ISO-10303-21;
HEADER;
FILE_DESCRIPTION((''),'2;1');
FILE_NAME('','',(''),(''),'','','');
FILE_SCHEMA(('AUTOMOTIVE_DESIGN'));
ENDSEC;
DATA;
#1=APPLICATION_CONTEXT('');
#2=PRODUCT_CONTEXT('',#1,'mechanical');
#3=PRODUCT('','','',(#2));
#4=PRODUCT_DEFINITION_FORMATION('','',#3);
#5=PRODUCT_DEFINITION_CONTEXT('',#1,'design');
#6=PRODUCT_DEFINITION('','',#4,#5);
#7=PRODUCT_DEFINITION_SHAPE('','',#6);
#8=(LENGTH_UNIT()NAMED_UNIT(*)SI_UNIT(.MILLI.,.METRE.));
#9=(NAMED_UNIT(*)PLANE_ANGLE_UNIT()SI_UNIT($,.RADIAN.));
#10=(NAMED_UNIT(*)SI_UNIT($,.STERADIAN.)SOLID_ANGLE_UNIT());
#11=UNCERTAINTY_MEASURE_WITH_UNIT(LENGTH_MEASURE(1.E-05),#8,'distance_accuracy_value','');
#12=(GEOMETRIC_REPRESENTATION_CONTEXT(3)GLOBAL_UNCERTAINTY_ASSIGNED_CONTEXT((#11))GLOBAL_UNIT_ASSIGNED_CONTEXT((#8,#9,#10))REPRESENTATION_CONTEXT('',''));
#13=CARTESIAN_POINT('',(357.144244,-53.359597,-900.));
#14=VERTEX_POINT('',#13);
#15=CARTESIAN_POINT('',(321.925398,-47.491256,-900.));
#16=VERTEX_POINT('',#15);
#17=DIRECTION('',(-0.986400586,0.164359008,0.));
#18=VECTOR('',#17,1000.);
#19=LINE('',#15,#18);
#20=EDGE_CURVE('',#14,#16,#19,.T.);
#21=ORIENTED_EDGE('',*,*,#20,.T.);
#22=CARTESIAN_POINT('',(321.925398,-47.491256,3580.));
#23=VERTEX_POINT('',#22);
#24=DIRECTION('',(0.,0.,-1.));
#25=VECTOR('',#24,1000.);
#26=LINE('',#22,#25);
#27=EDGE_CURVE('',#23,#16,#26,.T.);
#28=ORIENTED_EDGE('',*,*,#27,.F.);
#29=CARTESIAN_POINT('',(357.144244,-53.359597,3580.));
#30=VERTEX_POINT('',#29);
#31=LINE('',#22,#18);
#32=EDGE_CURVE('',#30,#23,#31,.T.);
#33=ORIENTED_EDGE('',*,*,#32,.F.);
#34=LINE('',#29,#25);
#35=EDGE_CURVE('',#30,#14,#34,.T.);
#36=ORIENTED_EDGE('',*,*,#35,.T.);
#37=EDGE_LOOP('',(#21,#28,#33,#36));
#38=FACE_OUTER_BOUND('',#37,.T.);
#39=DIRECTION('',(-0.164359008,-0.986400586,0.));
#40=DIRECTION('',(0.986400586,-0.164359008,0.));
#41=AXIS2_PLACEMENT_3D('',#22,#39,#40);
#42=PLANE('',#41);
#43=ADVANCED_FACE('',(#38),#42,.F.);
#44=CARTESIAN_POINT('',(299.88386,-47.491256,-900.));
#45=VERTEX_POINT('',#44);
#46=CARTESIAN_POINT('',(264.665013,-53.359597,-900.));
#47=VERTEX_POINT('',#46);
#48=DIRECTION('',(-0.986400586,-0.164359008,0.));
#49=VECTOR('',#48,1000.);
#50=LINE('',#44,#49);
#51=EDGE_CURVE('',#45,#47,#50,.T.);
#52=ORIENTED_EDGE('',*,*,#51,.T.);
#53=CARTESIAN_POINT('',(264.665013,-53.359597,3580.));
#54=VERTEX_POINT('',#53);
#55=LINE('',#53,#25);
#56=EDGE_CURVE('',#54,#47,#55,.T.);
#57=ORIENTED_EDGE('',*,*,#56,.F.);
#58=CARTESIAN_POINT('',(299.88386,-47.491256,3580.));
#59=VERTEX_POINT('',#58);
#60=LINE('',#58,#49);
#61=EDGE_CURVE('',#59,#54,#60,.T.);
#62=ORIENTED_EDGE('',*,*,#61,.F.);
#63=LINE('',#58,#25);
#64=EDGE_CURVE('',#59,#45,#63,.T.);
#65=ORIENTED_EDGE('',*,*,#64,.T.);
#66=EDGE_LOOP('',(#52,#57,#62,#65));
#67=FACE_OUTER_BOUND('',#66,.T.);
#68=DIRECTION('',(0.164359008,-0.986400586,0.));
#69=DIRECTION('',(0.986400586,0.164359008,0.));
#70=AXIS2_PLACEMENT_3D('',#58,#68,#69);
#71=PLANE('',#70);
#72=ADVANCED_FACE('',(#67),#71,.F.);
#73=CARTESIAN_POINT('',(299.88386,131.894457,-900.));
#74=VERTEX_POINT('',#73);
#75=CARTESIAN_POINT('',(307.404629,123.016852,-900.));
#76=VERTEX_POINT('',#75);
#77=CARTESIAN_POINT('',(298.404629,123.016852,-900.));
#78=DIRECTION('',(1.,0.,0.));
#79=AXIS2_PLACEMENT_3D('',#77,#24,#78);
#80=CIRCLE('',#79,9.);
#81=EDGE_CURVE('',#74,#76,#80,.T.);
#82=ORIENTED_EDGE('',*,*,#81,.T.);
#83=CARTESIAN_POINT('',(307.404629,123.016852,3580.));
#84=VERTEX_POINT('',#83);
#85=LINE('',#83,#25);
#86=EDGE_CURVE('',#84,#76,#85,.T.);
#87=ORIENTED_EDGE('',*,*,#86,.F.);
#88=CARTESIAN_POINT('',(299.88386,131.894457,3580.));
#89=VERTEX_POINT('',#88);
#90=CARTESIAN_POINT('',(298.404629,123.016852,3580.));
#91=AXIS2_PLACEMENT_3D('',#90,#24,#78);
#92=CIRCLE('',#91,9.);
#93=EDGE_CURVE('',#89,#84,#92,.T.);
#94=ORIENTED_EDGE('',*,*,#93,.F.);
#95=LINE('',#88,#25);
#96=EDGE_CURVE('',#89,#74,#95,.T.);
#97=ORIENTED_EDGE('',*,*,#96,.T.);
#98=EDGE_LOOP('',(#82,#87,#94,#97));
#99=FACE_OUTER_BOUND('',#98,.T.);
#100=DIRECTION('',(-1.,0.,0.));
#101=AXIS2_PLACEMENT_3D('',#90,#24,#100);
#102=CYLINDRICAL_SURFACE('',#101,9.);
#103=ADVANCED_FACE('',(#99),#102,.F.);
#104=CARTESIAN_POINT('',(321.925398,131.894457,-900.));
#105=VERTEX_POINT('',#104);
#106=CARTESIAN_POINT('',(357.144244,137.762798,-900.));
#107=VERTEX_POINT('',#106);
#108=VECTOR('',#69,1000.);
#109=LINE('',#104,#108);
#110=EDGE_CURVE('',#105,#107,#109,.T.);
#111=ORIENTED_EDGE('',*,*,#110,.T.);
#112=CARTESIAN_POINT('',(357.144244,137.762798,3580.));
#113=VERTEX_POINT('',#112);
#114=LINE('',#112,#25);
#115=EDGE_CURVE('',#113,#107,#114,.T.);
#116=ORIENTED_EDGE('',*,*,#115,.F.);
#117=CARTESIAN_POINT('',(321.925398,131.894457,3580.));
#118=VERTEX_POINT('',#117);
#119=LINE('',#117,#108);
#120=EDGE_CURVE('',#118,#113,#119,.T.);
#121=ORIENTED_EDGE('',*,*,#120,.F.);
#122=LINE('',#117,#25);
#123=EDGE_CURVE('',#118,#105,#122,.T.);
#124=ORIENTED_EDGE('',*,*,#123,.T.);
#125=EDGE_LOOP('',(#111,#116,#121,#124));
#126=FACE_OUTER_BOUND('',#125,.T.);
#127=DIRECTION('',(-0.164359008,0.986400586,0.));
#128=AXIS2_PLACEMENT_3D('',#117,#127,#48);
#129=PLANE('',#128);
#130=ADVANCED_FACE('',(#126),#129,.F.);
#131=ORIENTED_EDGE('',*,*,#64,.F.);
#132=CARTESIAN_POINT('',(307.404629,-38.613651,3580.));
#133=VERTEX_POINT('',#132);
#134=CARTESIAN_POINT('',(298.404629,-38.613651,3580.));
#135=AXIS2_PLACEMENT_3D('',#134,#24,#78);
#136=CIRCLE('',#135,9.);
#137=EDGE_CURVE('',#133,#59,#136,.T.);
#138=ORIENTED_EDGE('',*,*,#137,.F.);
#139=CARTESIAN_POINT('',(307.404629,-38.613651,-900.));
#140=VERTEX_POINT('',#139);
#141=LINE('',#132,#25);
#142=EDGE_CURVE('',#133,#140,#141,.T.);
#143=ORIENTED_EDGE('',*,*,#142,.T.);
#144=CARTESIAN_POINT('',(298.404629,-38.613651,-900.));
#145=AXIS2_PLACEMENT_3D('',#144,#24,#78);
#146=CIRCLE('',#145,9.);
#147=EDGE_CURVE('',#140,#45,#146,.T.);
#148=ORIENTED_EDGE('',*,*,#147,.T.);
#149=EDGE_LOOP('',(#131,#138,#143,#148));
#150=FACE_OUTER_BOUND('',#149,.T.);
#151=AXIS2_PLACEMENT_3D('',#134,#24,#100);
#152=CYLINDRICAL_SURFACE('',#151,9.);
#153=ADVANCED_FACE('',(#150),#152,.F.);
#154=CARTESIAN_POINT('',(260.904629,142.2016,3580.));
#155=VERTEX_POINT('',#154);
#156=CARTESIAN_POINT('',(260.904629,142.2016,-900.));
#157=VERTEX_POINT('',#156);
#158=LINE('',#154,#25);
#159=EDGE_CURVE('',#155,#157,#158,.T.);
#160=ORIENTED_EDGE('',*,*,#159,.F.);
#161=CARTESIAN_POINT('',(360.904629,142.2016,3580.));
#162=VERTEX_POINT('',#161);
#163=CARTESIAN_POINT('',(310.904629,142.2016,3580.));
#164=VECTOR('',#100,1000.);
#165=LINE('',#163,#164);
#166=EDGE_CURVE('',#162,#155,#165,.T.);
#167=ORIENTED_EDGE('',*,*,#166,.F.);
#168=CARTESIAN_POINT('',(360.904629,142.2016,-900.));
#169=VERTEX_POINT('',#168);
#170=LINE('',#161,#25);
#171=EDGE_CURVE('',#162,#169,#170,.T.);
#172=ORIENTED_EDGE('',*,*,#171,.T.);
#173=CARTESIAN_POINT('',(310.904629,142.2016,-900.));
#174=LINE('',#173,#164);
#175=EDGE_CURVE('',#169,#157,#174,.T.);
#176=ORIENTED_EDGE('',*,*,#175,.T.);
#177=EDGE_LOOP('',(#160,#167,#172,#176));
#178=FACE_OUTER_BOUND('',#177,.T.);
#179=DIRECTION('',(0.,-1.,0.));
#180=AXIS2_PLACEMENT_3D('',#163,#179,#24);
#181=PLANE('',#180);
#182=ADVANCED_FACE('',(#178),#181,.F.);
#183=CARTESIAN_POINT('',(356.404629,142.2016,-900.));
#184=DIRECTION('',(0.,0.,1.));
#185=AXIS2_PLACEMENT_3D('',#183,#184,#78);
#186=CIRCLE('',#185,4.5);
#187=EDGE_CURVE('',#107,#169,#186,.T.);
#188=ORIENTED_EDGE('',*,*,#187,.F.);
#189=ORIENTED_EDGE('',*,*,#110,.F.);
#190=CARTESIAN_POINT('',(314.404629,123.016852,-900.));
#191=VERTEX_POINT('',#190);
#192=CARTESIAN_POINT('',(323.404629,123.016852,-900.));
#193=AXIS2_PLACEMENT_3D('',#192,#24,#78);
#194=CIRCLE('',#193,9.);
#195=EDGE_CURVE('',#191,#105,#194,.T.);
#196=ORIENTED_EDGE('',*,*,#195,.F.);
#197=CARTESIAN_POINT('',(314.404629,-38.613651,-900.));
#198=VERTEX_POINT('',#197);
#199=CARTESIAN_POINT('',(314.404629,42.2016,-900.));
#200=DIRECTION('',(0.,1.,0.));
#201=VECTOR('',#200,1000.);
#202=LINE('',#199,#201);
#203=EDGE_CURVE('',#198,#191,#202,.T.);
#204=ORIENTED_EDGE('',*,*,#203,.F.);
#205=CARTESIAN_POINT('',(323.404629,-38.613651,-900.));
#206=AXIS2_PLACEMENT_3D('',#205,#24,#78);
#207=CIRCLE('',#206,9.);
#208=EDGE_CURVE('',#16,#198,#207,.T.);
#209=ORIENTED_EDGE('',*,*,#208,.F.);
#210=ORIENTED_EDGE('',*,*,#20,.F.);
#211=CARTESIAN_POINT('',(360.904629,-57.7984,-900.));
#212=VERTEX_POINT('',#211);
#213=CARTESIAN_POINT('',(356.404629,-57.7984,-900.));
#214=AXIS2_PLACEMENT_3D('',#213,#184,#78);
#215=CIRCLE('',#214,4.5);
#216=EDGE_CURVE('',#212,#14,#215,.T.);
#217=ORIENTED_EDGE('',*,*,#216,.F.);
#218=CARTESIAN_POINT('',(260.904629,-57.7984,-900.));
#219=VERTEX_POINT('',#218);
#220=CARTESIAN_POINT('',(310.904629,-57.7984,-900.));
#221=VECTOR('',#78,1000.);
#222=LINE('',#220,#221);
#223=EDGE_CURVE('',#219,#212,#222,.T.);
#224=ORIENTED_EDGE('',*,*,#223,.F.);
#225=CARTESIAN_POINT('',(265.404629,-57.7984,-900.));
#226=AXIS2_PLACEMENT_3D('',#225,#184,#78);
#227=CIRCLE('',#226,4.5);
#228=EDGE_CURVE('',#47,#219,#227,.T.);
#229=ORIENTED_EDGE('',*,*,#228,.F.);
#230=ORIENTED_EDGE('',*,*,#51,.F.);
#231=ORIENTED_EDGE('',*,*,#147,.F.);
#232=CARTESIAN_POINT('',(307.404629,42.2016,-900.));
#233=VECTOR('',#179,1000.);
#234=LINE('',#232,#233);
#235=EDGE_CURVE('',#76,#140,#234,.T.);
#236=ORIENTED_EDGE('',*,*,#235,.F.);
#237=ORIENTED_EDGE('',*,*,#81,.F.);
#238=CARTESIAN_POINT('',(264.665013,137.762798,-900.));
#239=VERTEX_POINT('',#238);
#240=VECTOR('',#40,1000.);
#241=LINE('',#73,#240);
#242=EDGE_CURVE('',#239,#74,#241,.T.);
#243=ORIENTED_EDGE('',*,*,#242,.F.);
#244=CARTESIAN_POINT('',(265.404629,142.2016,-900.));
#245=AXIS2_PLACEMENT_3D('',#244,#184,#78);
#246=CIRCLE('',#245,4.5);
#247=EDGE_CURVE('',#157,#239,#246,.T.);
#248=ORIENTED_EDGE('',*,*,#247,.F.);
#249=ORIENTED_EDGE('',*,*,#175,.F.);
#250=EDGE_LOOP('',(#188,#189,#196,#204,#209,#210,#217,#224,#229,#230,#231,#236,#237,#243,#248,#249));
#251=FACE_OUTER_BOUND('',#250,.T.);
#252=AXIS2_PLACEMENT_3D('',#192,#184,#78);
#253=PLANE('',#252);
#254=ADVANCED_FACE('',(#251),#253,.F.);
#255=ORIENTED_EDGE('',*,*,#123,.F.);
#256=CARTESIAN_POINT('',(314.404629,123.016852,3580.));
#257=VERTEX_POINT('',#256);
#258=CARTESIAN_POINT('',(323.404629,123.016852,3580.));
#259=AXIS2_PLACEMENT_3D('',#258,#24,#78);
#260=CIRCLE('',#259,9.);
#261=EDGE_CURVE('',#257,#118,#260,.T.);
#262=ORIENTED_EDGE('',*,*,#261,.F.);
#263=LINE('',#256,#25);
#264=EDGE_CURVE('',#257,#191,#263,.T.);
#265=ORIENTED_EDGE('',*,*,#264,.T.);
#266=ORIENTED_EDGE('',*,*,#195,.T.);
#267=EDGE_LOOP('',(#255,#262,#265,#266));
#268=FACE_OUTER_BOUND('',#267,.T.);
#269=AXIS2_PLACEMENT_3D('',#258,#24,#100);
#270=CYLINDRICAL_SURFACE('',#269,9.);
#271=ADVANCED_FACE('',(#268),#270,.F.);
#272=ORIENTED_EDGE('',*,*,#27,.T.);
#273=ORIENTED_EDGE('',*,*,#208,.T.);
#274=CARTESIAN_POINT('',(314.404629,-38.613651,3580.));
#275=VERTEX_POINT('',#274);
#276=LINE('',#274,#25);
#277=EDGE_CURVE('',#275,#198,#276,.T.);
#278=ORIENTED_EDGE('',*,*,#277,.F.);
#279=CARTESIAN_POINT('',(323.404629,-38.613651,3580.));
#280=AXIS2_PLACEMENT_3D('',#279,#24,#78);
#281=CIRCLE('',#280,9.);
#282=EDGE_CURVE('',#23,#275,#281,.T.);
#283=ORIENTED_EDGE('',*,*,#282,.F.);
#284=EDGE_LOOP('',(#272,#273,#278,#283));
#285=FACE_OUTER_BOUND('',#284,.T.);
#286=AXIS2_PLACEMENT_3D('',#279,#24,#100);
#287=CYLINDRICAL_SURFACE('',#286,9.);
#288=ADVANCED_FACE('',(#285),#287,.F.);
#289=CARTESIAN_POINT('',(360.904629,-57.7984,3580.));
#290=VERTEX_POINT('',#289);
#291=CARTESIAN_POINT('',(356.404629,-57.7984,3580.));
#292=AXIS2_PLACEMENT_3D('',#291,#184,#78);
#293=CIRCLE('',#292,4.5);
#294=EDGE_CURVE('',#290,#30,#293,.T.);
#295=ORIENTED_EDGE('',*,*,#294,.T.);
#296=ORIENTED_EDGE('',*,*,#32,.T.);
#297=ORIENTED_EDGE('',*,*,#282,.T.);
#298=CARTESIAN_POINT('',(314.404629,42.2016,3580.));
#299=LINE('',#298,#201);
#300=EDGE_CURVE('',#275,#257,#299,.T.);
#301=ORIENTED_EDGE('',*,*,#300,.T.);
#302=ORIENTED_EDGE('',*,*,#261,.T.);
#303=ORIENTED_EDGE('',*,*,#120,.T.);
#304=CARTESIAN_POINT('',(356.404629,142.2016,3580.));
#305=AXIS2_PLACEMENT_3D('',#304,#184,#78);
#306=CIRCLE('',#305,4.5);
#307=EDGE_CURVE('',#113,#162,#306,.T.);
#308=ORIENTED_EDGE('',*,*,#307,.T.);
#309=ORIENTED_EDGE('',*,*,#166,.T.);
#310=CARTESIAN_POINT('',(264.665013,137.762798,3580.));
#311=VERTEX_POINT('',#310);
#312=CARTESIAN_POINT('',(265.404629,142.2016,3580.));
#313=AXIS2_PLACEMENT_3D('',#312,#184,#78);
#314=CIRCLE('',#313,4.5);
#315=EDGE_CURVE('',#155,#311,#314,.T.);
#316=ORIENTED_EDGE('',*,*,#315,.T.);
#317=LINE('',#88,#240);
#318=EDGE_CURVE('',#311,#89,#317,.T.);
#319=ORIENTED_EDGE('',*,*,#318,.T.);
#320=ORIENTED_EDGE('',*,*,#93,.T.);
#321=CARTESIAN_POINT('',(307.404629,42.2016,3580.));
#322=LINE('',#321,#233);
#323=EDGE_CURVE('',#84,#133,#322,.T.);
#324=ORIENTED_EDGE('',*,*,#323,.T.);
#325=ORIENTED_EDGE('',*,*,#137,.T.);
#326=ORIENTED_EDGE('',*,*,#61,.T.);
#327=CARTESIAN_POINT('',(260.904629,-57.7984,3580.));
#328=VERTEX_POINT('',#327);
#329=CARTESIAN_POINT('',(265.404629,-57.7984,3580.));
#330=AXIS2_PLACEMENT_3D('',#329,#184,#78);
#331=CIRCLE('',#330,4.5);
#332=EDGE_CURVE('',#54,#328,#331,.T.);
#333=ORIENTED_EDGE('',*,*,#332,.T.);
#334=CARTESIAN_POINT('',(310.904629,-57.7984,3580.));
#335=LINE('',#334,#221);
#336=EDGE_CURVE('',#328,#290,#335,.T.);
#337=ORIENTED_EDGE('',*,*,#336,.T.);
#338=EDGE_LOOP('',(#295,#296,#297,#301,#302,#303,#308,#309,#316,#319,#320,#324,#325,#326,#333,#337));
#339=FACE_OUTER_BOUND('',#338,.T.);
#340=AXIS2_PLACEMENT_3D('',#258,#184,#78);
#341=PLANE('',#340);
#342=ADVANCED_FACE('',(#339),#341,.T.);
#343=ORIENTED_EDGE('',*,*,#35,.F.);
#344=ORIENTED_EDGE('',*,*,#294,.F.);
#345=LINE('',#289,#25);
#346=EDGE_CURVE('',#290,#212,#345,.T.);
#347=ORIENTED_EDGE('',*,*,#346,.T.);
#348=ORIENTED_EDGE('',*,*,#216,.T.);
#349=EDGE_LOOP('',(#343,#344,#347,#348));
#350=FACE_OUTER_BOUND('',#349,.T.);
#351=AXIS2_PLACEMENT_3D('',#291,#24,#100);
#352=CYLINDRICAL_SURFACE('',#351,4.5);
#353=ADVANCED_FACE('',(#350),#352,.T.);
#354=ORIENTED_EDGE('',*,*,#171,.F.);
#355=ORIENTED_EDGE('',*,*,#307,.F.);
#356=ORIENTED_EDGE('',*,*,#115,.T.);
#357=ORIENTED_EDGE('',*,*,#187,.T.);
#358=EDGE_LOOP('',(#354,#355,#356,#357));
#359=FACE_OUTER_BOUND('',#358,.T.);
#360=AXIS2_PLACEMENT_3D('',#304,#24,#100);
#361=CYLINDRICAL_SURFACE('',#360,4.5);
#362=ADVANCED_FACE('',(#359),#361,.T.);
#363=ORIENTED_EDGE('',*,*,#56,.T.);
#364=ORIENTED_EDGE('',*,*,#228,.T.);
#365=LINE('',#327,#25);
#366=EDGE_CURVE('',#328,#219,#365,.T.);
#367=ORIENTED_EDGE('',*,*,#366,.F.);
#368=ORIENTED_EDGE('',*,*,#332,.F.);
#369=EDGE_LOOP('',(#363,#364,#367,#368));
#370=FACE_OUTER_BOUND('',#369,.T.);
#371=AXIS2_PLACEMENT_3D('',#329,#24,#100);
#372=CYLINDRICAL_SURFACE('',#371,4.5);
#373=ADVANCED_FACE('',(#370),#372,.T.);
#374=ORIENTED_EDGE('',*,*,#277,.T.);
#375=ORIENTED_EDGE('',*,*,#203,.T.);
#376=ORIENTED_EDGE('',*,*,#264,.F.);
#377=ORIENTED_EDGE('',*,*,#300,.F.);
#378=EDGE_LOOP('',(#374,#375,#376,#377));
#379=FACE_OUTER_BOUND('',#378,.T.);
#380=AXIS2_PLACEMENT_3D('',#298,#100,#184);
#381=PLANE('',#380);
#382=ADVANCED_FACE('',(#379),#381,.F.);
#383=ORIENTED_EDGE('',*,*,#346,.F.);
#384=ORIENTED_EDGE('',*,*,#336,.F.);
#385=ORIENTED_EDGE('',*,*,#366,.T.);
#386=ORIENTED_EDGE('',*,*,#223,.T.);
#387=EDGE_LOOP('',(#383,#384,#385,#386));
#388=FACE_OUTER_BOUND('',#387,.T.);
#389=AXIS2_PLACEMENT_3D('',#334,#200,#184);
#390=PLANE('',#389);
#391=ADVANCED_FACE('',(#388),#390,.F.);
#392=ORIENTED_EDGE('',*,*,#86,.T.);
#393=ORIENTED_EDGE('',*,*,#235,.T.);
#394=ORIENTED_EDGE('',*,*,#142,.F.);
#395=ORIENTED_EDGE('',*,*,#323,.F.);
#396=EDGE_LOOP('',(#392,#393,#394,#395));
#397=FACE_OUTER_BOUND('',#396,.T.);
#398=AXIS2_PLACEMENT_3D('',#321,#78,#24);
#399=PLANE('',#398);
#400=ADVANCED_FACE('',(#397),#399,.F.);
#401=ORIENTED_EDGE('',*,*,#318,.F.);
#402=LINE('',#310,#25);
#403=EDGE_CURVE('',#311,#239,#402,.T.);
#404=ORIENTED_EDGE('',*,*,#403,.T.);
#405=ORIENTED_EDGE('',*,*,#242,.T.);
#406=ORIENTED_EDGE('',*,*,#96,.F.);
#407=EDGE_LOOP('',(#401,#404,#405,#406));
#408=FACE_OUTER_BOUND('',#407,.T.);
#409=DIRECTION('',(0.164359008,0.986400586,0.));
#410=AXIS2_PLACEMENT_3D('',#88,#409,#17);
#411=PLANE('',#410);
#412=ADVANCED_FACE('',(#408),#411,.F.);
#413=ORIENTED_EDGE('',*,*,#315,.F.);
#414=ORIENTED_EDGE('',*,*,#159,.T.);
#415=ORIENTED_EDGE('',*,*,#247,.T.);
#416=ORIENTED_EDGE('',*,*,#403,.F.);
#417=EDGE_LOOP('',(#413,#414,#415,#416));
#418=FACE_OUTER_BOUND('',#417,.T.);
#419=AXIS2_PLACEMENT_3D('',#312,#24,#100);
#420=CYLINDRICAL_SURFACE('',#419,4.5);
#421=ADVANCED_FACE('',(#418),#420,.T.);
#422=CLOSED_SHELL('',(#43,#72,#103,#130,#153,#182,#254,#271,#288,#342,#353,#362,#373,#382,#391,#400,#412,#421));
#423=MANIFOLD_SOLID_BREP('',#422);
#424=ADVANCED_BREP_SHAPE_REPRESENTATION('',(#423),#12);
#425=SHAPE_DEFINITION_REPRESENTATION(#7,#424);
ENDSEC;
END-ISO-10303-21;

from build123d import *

# Parameters (mm, degrees)
BOSS_EXTRUDE1_DEPTH = 3580
MOVE_FACE1_BY       = 900


with BuildPart() as part:
    # Sketch1 → Boss-Extrude1 (new body)
    with BuildSketch(Plane.XY):
        with BuildLine():
            Line((314.404628659, 42.201600466), (314.404628659, -38.613650919))
            ThreePointArc((314.404628659, -38.613650919), (316.537566708, -44.431164147), (321.925397583, -47.491256194))
            Line((321.925397583, -47.491256194), (357.144244197, -53.359596897))
            ThreePointArc((357.144244197, -53.359596897), (359.838159635, -54.88964292), (360.904628659, -57.798399534))
            Line((360.904628659, -57.798399534), (310.904628659, -57.798399534))
            Line((310.904628659, -57.798399534), (260.904628659, -57.798399534))
            ThreePointArc((260.904628659, -57.798399534), (261.971097684, -54.88964292), (264.665013121, -53.359596897))
            Line((264.665013121, -53.359596897), (299.883859735, -47.491256194))
            ThreePointArc((299.883859735, -47.491256194), (305.27169061, -44.431164147), (307.404628659, -38.613650919))
            Line((307.404628659, -38.613650919), (307.404628659, 42.201600466))
            Line((307.404628659, 42.201600466), (307.404628659, 123.016851851))
            ThreePointArc((307.404628659, 123.016851851), (305.27169061, 128.834365079), (299.883859735, 131.894457126))
            Line((299.883859735, 131.894457126), (264.665013121, 137.762797828))
            ThreePointArc((264.665013121, 137.762797828), (261.971097684, 139.292843852), (260.904628659, 142.201600466))
            Line((260.904628659, 142.201600466), (310.904628659, 142.201600466))
            Line((310.904628659, 142.201600466), (360.904628659, 142.201600466))
            ThreePointArc((360.904628659, 142.201600466), (359.838159635, 139.292843852), (357.144244197, 137.762797828))
            Line((357.144244197, 137.762797828), (321.925397583, 131.894457126))
            ThreePointArc((321.925397583, 131.894457126), (316.537566708, 128.834365079), (314.404628659, 123.016851851))
            Line((314.404628659, 123.016851851), (314.404628659, 42.201600466))
        make_face()
    extrude(amount=BOSS_EXTRUDE1_DEPTH)

    # Move Face1: a face moved outward by 900.0
    extrude(part.faces().sort_by_distance((310.904628659, 42.201600466, 0))[0], amount=MOVE_FACE1_BY, dir=(0, 0, -1))


solid = part.part
